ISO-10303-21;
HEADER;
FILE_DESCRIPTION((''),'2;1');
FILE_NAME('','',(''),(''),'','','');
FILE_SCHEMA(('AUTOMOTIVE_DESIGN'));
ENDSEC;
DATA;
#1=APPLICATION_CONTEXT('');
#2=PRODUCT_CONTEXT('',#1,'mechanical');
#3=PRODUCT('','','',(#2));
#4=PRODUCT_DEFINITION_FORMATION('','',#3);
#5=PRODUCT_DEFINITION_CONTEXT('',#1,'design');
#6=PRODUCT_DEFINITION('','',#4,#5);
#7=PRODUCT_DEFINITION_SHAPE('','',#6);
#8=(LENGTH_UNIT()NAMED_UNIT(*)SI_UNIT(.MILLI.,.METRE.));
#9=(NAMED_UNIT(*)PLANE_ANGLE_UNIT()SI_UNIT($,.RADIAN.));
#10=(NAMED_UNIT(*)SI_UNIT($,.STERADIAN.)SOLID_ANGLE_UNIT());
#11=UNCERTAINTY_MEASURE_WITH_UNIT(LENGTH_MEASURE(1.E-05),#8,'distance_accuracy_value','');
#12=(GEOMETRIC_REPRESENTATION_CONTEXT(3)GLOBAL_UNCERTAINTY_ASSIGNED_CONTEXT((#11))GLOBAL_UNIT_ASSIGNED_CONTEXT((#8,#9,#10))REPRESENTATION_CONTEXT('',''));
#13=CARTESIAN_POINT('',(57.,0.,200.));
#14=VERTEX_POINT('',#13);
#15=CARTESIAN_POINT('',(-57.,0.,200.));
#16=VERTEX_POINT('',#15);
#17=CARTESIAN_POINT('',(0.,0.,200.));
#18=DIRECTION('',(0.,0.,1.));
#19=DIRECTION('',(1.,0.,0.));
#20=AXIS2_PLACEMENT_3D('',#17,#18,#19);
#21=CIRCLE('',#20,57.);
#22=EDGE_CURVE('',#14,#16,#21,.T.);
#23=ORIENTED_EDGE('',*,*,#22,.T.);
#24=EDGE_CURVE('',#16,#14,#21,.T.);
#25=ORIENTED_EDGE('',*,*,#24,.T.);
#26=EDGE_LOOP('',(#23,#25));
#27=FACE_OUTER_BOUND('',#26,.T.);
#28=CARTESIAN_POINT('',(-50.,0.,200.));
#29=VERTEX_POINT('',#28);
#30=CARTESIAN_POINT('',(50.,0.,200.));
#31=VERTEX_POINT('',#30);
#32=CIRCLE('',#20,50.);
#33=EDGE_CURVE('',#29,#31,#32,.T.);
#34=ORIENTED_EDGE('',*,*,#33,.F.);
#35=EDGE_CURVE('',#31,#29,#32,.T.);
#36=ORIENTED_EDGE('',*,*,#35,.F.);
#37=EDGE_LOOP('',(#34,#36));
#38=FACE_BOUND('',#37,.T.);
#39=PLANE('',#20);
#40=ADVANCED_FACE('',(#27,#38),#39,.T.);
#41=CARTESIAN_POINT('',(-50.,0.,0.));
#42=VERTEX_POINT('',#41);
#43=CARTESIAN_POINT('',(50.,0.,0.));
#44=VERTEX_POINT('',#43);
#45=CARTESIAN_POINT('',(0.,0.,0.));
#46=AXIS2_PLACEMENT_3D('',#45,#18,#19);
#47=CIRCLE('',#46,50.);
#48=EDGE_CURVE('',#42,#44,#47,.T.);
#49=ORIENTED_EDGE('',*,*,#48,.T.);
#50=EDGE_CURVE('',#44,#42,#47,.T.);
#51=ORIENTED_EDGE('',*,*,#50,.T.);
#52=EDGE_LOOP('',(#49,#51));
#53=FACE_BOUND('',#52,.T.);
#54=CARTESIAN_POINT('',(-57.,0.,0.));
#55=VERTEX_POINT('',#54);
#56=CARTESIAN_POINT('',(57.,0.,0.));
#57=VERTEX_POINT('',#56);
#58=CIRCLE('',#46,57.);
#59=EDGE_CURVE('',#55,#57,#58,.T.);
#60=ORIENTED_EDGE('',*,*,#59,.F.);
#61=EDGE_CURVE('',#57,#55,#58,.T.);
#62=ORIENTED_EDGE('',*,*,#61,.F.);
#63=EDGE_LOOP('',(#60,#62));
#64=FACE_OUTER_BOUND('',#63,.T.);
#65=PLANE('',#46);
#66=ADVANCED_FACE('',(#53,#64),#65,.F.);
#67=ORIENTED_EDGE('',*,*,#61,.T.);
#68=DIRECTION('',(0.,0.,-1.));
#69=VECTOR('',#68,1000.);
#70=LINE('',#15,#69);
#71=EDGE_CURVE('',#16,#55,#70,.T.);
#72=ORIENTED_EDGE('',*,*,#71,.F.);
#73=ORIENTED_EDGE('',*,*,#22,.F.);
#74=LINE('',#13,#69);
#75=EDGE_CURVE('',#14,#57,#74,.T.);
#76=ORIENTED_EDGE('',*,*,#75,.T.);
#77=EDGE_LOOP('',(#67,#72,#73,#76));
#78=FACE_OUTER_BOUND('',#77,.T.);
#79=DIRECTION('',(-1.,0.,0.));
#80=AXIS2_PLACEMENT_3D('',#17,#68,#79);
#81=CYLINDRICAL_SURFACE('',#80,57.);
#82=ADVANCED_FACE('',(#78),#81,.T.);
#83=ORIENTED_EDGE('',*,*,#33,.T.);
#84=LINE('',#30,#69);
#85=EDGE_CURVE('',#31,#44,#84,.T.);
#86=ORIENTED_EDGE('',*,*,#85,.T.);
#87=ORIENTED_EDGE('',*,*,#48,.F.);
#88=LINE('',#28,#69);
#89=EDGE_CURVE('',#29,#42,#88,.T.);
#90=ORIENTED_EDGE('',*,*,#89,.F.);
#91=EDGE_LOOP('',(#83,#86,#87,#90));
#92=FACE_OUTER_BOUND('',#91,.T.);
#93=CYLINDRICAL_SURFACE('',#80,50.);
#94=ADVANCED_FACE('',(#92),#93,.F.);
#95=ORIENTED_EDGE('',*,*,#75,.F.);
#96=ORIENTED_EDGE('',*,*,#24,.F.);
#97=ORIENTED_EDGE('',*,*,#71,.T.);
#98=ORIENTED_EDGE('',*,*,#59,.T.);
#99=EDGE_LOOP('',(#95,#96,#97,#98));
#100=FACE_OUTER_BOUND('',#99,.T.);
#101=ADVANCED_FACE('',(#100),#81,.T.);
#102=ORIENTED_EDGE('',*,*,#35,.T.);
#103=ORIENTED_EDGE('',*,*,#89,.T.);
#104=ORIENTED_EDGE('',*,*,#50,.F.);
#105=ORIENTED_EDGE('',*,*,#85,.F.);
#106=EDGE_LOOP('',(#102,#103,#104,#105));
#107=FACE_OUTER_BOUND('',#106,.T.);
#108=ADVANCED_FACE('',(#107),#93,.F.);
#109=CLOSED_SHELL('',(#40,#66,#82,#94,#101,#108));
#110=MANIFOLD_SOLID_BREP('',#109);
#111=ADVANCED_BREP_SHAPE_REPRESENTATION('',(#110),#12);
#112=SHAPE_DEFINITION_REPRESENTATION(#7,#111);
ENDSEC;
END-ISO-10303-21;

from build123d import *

# Parameters (mm, degrees)
SKETCH1_R           = 57
SKETCH1_R_2         = 50
BOSS_EXTRUDE1_DEPTH = 200


with BuildPart() as part:
    # Sketch1 → Boss-Extrude1 (new body)
    with BuildSketch(Plane.XY):
        Circle(SKETCH1_R)
        Circle(SKETCH1_R_2, mode=Mode.SUBTRACT)
    extrude(amount=BOSS_EXTRUDE1_DEPTH)


solid = part.part
